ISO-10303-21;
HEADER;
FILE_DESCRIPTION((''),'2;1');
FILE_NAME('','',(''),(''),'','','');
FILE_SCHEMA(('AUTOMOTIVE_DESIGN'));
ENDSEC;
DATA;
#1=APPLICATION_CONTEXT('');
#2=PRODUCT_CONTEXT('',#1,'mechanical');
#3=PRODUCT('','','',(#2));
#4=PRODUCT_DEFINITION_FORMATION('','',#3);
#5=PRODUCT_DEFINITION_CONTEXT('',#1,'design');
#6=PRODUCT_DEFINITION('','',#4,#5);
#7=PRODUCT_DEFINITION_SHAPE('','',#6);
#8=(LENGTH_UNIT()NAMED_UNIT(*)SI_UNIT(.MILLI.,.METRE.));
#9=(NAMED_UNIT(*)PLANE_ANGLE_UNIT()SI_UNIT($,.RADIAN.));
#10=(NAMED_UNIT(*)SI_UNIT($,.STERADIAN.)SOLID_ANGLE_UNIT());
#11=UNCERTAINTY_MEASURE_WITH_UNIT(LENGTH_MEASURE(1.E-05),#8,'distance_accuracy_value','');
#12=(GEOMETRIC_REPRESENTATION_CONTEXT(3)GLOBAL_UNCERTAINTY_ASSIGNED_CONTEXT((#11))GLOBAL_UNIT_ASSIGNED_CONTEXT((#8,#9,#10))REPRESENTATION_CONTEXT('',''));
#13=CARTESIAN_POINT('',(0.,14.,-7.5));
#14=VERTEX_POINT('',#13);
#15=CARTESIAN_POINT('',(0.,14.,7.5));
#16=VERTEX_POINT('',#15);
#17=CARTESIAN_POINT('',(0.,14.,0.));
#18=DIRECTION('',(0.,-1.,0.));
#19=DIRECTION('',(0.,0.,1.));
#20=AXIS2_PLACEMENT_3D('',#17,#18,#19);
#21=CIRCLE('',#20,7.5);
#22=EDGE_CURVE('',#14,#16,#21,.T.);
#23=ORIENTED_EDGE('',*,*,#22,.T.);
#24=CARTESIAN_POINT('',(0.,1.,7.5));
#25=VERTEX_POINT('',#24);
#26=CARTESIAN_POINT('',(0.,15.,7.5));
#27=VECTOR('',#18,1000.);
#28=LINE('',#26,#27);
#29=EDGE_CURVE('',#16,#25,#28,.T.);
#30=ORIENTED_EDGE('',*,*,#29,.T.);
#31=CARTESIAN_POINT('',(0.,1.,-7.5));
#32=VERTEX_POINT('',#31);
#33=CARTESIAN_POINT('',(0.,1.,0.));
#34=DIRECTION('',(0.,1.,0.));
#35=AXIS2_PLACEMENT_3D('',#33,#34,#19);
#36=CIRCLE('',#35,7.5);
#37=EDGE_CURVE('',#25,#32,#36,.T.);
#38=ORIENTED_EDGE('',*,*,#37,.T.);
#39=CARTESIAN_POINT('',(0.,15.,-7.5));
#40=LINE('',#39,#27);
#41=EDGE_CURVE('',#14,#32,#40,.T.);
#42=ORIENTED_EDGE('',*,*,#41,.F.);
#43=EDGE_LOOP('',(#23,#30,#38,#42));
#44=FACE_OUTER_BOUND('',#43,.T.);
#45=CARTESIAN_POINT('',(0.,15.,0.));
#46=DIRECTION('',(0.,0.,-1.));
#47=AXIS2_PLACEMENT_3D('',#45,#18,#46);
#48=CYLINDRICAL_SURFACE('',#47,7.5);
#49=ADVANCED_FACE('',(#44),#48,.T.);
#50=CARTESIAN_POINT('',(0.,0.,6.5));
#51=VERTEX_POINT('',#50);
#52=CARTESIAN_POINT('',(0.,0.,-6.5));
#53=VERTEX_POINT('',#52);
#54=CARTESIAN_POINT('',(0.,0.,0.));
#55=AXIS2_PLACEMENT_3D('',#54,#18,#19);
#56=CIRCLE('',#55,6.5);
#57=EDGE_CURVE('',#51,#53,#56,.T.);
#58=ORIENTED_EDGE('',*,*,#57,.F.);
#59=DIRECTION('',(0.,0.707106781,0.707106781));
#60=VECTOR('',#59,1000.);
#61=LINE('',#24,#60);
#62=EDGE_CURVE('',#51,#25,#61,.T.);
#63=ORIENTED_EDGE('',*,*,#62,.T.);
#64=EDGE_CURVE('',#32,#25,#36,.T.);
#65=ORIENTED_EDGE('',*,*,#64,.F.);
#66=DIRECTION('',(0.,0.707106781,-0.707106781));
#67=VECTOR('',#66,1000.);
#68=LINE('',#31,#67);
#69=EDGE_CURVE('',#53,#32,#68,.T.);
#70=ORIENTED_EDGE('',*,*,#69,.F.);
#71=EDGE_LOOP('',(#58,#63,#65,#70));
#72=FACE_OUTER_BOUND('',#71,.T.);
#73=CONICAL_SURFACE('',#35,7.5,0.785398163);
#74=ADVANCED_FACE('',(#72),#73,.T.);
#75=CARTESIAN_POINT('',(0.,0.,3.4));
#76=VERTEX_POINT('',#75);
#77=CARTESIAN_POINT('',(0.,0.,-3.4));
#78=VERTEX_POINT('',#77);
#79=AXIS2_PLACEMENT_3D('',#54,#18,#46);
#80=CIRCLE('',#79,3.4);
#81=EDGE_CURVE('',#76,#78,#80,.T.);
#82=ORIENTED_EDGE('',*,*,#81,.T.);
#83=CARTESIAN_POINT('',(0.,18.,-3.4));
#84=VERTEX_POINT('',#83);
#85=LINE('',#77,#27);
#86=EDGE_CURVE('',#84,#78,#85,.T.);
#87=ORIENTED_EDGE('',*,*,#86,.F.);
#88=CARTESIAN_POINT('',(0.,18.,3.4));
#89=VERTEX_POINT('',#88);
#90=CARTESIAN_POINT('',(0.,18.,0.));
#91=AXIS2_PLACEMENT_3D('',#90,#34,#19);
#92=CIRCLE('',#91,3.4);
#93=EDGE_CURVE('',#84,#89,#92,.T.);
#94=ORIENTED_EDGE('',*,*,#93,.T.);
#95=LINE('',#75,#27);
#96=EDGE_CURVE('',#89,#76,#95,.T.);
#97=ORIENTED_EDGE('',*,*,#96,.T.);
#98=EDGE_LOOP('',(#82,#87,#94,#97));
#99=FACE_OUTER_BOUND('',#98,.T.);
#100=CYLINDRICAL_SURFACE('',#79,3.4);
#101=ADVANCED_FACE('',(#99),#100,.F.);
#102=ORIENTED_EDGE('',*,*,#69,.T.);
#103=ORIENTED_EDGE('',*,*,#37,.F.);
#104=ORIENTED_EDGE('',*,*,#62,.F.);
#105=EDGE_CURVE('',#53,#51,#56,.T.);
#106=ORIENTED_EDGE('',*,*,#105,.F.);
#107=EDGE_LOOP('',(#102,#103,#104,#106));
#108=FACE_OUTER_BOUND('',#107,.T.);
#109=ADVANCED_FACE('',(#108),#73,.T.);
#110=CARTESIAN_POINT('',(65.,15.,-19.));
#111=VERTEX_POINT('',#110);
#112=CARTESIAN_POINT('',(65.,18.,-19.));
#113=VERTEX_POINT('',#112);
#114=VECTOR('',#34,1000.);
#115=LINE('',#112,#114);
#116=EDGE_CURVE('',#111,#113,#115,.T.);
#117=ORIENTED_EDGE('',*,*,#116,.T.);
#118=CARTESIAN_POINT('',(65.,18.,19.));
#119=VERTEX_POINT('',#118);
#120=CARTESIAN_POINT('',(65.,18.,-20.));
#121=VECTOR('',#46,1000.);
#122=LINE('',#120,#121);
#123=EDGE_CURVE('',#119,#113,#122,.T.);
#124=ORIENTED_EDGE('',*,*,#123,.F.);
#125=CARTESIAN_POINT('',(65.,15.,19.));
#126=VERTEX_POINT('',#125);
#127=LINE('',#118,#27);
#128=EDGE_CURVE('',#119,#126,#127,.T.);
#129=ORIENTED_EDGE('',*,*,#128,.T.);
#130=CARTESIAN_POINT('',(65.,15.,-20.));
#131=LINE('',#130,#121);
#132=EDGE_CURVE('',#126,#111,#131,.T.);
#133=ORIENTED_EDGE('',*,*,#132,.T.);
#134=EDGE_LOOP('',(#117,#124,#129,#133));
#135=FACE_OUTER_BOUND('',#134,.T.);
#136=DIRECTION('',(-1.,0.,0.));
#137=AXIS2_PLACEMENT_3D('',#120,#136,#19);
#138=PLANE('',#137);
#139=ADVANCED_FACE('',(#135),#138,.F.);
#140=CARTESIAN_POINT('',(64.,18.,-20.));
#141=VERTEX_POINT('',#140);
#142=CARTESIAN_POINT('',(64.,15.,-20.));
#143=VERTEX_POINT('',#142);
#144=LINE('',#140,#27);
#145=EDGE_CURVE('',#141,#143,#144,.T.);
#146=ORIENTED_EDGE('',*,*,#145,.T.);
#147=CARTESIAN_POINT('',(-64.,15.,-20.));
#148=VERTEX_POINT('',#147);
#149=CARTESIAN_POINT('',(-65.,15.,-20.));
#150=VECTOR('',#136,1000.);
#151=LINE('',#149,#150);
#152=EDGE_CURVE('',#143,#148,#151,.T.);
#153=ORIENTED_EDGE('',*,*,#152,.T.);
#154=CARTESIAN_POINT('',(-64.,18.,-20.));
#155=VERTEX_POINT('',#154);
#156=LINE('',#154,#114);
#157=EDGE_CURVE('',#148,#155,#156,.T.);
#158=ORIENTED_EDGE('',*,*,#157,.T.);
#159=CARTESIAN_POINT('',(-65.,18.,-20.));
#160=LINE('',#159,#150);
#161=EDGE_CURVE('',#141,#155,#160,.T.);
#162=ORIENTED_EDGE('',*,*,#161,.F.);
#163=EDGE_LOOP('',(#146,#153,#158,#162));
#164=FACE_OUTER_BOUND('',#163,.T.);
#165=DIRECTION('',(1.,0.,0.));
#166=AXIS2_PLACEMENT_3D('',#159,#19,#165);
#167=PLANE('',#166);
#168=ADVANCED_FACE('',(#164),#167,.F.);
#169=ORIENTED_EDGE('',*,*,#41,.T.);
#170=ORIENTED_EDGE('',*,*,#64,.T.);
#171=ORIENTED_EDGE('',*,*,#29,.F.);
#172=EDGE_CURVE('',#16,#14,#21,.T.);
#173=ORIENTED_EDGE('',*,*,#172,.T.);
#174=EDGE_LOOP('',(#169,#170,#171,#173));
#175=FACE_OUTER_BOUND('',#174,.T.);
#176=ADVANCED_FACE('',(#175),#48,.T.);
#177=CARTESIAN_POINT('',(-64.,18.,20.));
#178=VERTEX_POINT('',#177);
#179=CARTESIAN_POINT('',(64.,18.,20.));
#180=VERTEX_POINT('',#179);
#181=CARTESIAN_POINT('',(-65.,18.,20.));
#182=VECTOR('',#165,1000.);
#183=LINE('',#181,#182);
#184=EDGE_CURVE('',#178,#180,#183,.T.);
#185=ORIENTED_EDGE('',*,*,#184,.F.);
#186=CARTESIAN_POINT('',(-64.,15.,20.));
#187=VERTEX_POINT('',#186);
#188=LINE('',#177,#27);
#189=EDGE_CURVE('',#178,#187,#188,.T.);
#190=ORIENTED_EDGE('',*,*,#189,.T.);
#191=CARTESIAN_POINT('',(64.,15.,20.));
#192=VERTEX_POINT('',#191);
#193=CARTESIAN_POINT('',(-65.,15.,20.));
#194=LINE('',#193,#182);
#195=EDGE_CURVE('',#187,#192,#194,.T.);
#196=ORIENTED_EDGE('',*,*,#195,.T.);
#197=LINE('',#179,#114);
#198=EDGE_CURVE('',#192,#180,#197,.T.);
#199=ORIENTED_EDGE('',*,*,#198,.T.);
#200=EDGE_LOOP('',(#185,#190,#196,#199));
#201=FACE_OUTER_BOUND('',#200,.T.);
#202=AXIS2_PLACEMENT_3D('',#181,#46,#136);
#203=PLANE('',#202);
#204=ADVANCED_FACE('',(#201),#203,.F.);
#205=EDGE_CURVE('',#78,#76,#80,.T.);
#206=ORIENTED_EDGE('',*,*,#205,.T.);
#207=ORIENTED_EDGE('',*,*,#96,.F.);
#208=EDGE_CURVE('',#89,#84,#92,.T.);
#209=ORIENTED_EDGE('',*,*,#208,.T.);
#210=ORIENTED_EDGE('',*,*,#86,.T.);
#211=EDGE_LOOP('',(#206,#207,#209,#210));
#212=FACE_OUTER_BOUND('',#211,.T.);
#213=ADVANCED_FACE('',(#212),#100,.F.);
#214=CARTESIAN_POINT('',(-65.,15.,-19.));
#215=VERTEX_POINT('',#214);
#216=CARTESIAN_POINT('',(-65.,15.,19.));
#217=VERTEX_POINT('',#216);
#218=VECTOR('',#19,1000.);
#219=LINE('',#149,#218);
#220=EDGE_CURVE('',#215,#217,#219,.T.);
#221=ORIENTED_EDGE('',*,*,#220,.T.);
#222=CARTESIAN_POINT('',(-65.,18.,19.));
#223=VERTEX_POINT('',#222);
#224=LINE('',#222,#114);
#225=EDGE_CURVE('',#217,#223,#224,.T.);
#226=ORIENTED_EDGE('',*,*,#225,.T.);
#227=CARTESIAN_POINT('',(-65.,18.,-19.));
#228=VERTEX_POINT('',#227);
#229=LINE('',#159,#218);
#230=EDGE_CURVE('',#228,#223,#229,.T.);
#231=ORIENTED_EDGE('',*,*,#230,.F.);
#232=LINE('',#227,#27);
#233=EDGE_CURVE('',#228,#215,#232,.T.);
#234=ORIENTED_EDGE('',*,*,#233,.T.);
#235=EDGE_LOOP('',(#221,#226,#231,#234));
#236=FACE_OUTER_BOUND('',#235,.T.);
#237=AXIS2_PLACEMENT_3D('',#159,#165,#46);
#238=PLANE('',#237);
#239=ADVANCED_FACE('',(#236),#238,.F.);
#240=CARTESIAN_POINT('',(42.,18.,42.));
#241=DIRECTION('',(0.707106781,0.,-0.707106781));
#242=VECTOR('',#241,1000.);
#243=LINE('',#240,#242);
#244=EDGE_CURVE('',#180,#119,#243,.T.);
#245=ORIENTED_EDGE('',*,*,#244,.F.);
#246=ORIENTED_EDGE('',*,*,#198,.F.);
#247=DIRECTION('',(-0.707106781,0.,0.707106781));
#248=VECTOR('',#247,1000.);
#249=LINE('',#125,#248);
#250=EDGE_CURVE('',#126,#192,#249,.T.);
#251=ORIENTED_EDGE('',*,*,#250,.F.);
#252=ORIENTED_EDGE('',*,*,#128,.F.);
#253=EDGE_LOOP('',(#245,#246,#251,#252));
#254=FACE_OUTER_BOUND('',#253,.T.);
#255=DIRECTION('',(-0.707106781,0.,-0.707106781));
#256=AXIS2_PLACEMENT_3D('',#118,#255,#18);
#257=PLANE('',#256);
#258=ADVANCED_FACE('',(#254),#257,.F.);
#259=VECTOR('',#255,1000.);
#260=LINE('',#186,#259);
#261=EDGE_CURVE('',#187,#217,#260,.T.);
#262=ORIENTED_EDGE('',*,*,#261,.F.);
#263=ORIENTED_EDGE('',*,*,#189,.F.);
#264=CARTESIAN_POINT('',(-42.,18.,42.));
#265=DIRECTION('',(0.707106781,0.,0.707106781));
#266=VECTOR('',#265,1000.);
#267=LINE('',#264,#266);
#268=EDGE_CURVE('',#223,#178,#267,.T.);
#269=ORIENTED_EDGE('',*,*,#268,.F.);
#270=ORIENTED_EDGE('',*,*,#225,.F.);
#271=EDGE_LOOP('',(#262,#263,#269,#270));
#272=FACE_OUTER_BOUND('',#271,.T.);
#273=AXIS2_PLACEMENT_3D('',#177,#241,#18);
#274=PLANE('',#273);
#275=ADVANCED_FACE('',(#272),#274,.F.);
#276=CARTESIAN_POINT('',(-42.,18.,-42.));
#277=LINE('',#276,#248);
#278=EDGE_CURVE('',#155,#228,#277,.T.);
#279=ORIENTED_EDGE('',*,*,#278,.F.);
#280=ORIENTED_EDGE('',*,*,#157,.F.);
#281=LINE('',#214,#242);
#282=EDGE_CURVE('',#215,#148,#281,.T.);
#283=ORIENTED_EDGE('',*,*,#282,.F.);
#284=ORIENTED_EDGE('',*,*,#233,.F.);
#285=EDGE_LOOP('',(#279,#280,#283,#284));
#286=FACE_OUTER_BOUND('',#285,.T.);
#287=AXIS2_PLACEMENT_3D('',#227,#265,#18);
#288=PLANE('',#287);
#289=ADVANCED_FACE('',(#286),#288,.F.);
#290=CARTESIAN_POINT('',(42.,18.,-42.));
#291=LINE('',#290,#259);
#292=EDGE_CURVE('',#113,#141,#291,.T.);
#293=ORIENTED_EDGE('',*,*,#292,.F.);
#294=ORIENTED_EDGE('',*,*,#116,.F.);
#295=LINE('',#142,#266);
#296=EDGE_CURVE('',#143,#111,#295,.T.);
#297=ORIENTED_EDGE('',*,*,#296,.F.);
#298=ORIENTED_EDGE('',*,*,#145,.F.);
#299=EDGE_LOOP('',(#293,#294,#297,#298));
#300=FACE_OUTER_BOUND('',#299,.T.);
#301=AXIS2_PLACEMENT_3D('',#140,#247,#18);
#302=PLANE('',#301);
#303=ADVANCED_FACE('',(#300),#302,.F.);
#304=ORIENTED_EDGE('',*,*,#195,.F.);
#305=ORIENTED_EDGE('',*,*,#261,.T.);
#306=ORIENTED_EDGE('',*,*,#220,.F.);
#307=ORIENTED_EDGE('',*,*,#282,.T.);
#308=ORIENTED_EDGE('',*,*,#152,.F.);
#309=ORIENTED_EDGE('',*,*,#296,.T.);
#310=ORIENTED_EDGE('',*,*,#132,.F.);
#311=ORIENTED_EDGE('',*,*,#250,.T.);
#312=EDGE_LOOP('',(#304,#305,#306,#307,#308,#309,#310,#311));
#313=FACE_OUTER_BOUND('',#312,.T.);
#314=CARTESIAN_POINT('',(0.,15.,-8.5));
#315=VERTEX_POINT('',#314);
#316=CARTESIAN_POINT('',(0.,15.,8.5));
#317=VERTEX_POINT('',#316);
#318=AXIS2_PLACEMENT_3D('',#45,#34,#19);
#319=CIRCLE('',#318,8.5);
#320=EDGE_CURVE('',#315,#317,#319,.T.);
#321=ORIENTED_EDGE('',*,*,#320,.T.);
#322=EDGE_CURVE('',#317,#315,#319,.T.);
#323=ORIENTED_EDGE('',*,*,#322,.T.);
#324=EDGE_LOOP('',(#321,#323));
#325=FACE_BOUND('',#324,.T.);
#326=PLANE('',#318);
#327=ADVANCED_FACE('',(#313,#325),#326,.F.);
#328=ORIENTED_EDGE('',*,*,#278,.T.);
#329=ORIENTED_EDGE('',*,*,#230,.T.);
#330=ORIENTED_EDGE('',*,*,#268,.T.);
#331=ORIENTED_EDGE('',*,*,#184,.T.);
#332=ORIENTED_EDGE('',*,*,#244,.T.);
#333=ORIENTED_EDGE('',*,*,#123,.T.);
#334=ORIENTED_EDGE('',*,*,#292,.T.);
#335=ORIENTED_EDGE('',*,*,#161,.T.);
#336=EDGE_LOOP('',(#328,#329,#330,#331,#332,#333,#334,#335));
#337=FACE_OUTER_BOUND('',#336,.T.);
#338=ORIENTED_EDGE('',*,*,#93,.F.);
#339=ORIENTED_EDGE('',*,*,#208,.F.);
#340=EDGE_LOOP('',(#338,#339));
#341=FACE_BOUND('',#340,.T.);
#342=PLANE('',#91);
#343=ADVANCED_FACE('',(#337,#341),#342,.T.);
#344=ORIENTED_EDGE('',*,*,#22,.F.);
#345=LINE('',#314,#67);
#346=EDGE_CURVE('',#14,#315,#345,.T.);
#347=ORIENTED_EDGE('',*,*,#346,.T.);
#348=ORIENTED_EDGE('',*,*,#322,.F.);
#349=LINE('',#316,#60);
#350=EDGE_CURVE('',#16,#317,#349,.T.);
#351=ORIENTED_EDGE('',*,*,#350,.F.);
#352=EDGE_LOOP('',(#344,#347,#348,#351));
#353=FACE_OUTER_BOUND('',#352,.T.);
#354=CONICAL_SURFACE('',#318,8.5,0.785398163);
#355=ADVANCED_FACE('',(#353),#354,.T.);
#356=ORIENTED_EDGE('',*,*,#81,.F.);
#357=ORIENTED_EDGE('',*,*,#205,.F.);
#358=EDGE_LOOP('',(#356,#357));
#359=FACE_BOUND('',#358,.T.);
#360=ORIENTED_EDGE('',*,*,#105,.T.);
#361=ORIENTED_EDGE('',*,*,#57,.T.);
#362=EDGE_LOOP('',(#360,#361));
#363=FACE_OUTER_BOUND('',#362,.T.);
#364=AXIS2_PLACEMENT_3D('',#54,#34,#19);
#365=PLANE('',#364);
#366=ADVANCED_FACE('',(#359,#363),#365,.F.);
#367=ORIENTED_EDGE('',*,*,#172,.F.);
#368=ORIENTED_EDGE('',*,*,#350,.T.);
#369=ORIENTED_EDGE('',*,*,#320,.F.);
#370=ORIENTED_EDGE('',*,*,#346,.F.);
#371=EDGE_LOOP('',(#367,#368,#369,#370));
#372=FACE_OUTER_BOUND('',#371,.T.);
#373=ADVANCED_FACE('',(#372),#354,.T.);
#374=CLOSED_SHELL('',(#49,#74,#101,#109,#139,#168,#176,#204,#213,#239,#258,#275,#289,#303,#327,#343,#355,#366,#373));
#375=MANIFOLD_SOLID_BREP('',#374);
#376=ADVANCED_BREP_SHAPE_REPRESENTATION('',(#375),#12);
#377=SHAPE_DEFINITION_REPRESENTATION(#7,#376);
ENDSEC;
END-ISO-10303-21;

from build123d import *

# Parameters (mm, degrees)
SKETCH1_R             = 7.5
BOSS_EXTRUDE1_DEPTH   = 15
SKETCH2_W             = 130
SKETCH2_H             = 40
BOSS_EXTRUDE2_DEPTH   = 3
M8_TAPPED_HOLE1_D     = 6.8
M8_TAPPED_HOLE1_DEPTH = 19.75
M8_TAPPED_HOLE1_TIP   = 2.042926105
CHAMFER1_SIZE         = 1


with BuildPart() as part:
    # Sketch1 → Boss-Extrude1 (new body)
    with BuildSketch(Plane(origin=(0, 0, 0), x_dir=(1, 0, 0), z_dir=(0, 1, 0))):
        with Locations(Location((0, 0, 0), (0, 0, 270))):
            Circle(SKETCH1_R)
    extrude(amount=BOSS_EXTRUDE1_DEPTH)

    # Sketch2 → Boss-Extrude2 (add)
    with BuildSketch(Plane(origin=(0, 15, 0), x_dir=(1, 0, 0), z_dir=(0, 1, 0))):
        Rectangle(SKETCH2_W, SKETCH2_H)
    extrude(amount=BOSS_EXTRUDE2_DEPTH)

    # M8 Tapped Hole1
    with Locations(Plane(origin=(0, 0, 0), x_dir=(-1, 0, 0), z_dir=(0, -1, 0))):
        with Locations((0, 0)):
            Hole(M8_TAPPED_HOLE1_D / 2, depth=M8_TAPPED_HOLE1_DEPTH)
            with Locations((0, 0, -(M8_TAPPED_HOLE1_DEPTH + M8_TAPPED_HOLE1_TIP / 2))):  # 118° drill point
                Cone(0, M8_TAPPED_HOLE1_D / 2, M8_TAPPED_HOLE1_TIP, mode=Mode.SUBTRACT)

    # Chamfer1
    chamfer1_edges = [part.edges().sort_by_distance(p)[0] for p in [
        (0, 0, -7.5),
        (0, 15, -7.5),
        (65, 16.5, 20),
        (65, 16.5, -20),
        (-65, 16.5, -20),
        (-65, 16.5, 20),
    ]]
    chamfer(chamfer1_edges, length=CHAMFER1_SIZE)


solid = part.part
